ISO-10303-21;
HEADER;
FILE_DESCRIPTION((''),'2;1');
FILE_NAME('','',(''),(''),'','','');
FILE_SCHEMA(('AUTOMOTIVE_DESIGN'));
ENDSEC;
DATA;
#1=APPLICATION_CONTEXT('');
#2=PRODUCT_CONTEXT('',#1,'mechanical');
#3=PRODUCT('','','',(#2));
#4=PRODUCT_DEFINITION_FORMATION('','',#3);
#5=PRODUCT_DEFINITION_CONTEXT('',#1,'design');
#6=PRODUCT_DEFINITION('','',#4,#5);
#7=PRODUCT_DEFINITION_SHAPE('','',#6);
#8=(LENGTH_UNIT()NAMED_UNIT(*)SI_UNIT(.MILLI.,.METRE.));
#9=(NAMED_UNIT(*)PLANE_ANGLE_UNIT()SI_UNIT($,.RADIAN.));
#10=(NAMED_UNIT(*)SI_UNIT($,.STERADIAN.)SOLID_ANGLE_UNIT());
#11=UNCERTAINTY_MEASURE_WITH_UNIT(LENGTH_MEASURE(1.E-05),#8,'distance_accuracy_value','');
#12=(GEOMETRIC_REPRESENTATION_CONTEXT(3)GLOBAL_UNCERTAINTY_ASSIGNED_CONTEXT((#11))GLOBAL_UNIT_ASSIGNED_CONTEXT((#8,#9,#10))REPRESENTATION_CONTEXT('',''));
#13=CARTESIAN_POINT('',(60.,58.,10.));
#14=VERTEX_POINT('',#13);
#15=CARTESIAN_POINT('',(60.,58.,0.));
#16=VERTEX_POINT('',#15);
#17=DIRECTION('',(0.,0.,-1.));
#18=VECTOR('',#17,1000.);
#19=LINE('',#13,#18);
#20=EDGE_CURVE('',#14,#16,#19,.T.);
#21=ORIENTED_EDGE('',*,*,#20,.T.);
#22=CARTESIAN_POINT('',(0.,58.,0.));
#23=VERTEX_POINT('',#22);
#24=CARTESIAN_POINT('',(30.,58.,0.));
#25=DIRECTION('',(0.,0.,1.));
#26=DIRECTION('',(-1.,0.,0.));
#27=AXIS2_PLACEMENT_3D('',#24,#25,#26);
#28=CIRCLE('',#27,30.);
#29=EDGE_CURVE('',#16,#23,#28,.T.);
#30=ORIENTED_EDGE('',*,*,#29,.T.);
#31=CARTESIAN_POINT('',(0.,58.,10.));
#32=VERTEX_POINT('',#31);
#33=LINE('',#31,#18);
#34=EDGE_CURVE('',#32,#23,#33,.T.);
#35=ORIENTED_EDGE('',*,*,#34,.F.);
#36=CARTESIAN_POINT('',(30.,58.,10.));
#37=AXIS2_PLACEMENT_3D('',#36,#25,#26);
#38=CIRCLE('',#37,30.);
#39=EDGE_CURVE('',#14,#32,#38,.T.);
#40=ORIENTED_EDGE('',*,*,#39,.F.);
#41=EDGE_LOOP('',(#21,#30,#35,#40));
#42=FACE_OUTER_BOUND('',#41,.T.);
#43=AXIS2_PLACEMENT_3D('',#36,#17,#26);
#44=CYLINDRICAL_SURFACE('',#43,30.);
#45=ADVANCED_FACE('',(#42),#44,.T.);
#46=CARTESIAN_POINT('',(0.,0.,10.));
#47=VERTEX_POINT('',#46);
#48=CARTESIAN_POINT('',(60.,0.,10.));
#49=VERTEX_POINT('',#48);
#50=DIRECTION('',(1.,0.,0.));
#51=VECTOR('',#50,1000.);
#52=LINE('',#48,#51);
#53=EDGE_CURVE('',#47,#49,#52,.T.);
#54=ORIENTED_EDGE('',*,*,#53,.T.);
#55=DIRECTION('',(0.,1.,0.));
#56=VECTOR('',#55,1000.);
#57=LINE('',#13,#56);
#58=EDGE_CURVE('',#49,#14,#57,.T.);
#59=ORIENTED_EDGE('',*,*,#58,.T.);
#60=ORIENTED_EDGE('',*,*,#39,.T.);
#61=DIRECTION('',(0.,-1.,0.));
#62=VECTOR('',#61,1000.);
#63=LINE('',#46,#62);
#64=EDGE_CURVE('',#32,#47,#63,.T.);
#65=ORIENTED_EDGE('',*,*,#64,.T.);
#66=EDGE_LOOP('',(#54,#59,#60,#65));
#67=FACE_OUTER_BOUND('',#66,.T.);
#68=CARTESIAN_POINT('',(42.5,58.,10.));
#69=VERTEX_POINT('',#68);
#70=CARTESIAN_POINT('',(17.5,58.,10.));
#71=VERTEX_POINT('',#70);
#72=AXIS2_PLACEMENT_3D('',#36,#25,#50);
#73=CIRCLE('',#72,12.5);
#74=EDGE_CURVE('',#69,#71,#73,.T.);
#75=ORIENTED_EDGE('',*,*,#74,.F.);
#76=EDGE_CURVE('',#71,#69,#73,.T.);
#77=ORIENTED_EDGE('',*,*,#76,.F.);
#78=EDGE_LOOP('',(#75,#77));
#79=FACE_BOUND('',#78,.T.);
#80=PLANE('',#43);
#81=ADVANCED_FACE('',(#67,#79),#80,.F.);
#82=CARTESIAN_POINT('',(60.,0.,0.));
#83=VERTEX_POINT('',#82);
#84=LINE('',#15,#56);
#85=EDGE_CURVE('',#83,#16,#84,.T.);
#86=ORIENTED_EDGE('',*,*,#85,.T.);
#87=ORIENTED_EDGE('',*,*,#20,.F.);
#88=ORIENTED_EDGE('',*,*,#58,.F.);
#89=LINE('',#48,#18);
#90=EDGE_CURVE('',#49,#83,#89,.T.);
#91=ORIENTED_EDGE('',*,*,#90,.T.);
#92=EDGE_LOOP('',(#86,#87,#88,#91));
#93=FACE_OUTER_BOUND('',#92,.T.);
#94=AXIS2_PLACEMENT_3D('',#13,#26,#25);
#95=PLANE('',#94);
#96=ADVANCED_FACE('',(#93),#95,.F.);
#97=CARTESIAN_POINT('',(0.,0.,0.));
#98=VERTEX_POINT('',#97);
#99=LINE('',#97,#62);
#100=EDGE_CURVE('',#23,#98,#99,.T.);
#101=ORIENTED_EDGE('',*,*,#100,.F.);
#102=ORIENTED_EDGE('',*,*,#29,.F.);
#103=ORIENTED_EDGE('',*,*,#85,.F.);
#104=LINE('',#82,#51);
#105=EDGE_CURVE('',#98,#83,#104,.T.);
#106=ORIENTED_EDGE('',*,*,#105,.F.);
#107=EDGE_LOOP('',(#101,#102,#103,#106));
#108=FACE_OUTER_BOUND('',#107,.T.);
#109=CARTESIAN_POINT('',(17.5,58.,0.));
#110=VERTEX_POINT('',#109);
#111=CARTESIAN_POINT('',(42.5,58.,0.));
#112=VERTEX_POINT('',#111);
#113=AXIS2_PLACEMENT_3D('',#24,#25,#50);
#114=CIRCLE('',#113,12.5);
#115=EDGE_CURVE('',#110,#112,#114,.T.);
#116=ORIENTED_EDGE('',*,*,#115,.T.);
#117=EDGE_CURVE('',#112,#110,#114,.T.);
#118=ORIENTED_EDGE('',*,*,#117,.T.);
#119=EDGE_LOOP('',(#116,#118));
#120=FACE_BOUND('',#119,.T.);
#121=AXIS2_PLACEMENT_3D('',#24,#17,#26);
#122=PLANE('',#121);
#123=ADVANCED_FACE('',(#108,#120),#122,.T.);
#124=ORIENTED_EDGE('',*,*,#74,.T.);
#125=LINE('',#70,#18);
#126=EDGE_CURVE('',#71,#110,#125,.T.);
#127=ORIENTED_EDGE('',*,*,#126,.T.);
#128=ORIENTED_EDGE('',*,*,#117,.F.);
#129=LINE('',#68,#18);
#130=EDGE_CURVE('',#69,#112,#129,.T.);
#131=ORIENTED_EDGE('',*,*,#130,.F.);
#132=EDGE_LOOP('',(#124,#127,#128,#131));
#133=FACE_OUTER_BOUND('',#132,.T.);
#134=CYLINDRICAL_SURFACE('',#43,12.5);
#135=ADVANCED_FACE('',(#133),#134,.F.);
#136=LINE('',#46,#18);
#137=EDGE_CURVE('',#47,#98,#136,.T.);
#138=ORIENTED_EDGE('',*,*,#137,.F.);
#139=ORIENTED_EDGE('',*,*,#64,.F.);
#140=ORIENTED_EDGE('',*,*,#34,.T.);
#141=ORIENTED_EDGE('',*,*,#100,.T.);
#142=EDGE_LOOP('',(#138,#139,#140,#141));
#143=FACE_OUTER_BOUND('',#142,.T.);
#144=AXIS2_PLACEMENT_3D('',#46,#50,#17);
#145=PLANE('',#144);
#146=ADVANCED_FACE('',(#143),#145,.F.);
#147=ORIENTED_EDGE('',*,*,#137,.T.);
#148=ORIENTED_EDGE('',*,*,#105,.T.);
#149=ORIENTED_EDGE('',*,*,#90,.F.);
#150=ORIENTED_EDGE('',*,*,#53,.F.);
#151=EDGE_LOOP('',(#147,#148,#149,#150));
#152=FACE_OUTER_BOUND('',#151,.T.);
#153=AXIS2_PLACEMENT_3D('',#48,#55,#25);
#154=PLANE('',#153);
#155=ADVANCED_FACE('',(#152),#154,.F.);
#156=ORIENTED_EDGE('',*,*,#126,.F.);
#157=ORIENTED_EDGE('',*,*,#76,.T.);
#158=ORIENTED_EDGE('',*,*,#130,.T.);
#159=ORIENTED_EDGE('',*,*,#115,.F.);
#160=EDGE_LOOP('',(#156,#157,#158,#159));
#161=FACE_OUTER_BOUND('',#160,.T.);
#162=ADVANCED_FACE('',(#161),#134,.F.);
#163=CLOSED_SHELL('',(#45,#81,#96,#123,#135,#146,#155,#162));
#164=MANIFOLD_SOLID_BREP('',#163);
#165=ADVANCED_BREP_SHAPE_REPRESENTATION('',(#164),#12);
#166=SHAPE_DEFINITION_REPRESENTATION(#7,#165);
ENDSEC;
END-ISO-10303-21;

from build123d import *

# Parameters (mm, degrees)
SKETCH1_R           = 12.5
BOSS_EXTRUDE1_DEPTH = 10


with BuildPart() as part:
    # Sketch1 → Boss-Extrude1 (new body)
    with BuildSketch(Plane.XY):
        with BuildLine():
            Line((0, 0), (0, 58))
            ThreePointArc((0, 58), (30, 88), (60, 58))
            Line((60, 58), (60, 0))
            Line((60, 0), (0, 0))
        make_face()
        with Locations((30, 58)):
            Circle(SKETCH1_R, mode=Mode.SUBTRACT)
    extrude(amount=BOSS_EXTRUDE1_DEPTH)


solid = part.part
